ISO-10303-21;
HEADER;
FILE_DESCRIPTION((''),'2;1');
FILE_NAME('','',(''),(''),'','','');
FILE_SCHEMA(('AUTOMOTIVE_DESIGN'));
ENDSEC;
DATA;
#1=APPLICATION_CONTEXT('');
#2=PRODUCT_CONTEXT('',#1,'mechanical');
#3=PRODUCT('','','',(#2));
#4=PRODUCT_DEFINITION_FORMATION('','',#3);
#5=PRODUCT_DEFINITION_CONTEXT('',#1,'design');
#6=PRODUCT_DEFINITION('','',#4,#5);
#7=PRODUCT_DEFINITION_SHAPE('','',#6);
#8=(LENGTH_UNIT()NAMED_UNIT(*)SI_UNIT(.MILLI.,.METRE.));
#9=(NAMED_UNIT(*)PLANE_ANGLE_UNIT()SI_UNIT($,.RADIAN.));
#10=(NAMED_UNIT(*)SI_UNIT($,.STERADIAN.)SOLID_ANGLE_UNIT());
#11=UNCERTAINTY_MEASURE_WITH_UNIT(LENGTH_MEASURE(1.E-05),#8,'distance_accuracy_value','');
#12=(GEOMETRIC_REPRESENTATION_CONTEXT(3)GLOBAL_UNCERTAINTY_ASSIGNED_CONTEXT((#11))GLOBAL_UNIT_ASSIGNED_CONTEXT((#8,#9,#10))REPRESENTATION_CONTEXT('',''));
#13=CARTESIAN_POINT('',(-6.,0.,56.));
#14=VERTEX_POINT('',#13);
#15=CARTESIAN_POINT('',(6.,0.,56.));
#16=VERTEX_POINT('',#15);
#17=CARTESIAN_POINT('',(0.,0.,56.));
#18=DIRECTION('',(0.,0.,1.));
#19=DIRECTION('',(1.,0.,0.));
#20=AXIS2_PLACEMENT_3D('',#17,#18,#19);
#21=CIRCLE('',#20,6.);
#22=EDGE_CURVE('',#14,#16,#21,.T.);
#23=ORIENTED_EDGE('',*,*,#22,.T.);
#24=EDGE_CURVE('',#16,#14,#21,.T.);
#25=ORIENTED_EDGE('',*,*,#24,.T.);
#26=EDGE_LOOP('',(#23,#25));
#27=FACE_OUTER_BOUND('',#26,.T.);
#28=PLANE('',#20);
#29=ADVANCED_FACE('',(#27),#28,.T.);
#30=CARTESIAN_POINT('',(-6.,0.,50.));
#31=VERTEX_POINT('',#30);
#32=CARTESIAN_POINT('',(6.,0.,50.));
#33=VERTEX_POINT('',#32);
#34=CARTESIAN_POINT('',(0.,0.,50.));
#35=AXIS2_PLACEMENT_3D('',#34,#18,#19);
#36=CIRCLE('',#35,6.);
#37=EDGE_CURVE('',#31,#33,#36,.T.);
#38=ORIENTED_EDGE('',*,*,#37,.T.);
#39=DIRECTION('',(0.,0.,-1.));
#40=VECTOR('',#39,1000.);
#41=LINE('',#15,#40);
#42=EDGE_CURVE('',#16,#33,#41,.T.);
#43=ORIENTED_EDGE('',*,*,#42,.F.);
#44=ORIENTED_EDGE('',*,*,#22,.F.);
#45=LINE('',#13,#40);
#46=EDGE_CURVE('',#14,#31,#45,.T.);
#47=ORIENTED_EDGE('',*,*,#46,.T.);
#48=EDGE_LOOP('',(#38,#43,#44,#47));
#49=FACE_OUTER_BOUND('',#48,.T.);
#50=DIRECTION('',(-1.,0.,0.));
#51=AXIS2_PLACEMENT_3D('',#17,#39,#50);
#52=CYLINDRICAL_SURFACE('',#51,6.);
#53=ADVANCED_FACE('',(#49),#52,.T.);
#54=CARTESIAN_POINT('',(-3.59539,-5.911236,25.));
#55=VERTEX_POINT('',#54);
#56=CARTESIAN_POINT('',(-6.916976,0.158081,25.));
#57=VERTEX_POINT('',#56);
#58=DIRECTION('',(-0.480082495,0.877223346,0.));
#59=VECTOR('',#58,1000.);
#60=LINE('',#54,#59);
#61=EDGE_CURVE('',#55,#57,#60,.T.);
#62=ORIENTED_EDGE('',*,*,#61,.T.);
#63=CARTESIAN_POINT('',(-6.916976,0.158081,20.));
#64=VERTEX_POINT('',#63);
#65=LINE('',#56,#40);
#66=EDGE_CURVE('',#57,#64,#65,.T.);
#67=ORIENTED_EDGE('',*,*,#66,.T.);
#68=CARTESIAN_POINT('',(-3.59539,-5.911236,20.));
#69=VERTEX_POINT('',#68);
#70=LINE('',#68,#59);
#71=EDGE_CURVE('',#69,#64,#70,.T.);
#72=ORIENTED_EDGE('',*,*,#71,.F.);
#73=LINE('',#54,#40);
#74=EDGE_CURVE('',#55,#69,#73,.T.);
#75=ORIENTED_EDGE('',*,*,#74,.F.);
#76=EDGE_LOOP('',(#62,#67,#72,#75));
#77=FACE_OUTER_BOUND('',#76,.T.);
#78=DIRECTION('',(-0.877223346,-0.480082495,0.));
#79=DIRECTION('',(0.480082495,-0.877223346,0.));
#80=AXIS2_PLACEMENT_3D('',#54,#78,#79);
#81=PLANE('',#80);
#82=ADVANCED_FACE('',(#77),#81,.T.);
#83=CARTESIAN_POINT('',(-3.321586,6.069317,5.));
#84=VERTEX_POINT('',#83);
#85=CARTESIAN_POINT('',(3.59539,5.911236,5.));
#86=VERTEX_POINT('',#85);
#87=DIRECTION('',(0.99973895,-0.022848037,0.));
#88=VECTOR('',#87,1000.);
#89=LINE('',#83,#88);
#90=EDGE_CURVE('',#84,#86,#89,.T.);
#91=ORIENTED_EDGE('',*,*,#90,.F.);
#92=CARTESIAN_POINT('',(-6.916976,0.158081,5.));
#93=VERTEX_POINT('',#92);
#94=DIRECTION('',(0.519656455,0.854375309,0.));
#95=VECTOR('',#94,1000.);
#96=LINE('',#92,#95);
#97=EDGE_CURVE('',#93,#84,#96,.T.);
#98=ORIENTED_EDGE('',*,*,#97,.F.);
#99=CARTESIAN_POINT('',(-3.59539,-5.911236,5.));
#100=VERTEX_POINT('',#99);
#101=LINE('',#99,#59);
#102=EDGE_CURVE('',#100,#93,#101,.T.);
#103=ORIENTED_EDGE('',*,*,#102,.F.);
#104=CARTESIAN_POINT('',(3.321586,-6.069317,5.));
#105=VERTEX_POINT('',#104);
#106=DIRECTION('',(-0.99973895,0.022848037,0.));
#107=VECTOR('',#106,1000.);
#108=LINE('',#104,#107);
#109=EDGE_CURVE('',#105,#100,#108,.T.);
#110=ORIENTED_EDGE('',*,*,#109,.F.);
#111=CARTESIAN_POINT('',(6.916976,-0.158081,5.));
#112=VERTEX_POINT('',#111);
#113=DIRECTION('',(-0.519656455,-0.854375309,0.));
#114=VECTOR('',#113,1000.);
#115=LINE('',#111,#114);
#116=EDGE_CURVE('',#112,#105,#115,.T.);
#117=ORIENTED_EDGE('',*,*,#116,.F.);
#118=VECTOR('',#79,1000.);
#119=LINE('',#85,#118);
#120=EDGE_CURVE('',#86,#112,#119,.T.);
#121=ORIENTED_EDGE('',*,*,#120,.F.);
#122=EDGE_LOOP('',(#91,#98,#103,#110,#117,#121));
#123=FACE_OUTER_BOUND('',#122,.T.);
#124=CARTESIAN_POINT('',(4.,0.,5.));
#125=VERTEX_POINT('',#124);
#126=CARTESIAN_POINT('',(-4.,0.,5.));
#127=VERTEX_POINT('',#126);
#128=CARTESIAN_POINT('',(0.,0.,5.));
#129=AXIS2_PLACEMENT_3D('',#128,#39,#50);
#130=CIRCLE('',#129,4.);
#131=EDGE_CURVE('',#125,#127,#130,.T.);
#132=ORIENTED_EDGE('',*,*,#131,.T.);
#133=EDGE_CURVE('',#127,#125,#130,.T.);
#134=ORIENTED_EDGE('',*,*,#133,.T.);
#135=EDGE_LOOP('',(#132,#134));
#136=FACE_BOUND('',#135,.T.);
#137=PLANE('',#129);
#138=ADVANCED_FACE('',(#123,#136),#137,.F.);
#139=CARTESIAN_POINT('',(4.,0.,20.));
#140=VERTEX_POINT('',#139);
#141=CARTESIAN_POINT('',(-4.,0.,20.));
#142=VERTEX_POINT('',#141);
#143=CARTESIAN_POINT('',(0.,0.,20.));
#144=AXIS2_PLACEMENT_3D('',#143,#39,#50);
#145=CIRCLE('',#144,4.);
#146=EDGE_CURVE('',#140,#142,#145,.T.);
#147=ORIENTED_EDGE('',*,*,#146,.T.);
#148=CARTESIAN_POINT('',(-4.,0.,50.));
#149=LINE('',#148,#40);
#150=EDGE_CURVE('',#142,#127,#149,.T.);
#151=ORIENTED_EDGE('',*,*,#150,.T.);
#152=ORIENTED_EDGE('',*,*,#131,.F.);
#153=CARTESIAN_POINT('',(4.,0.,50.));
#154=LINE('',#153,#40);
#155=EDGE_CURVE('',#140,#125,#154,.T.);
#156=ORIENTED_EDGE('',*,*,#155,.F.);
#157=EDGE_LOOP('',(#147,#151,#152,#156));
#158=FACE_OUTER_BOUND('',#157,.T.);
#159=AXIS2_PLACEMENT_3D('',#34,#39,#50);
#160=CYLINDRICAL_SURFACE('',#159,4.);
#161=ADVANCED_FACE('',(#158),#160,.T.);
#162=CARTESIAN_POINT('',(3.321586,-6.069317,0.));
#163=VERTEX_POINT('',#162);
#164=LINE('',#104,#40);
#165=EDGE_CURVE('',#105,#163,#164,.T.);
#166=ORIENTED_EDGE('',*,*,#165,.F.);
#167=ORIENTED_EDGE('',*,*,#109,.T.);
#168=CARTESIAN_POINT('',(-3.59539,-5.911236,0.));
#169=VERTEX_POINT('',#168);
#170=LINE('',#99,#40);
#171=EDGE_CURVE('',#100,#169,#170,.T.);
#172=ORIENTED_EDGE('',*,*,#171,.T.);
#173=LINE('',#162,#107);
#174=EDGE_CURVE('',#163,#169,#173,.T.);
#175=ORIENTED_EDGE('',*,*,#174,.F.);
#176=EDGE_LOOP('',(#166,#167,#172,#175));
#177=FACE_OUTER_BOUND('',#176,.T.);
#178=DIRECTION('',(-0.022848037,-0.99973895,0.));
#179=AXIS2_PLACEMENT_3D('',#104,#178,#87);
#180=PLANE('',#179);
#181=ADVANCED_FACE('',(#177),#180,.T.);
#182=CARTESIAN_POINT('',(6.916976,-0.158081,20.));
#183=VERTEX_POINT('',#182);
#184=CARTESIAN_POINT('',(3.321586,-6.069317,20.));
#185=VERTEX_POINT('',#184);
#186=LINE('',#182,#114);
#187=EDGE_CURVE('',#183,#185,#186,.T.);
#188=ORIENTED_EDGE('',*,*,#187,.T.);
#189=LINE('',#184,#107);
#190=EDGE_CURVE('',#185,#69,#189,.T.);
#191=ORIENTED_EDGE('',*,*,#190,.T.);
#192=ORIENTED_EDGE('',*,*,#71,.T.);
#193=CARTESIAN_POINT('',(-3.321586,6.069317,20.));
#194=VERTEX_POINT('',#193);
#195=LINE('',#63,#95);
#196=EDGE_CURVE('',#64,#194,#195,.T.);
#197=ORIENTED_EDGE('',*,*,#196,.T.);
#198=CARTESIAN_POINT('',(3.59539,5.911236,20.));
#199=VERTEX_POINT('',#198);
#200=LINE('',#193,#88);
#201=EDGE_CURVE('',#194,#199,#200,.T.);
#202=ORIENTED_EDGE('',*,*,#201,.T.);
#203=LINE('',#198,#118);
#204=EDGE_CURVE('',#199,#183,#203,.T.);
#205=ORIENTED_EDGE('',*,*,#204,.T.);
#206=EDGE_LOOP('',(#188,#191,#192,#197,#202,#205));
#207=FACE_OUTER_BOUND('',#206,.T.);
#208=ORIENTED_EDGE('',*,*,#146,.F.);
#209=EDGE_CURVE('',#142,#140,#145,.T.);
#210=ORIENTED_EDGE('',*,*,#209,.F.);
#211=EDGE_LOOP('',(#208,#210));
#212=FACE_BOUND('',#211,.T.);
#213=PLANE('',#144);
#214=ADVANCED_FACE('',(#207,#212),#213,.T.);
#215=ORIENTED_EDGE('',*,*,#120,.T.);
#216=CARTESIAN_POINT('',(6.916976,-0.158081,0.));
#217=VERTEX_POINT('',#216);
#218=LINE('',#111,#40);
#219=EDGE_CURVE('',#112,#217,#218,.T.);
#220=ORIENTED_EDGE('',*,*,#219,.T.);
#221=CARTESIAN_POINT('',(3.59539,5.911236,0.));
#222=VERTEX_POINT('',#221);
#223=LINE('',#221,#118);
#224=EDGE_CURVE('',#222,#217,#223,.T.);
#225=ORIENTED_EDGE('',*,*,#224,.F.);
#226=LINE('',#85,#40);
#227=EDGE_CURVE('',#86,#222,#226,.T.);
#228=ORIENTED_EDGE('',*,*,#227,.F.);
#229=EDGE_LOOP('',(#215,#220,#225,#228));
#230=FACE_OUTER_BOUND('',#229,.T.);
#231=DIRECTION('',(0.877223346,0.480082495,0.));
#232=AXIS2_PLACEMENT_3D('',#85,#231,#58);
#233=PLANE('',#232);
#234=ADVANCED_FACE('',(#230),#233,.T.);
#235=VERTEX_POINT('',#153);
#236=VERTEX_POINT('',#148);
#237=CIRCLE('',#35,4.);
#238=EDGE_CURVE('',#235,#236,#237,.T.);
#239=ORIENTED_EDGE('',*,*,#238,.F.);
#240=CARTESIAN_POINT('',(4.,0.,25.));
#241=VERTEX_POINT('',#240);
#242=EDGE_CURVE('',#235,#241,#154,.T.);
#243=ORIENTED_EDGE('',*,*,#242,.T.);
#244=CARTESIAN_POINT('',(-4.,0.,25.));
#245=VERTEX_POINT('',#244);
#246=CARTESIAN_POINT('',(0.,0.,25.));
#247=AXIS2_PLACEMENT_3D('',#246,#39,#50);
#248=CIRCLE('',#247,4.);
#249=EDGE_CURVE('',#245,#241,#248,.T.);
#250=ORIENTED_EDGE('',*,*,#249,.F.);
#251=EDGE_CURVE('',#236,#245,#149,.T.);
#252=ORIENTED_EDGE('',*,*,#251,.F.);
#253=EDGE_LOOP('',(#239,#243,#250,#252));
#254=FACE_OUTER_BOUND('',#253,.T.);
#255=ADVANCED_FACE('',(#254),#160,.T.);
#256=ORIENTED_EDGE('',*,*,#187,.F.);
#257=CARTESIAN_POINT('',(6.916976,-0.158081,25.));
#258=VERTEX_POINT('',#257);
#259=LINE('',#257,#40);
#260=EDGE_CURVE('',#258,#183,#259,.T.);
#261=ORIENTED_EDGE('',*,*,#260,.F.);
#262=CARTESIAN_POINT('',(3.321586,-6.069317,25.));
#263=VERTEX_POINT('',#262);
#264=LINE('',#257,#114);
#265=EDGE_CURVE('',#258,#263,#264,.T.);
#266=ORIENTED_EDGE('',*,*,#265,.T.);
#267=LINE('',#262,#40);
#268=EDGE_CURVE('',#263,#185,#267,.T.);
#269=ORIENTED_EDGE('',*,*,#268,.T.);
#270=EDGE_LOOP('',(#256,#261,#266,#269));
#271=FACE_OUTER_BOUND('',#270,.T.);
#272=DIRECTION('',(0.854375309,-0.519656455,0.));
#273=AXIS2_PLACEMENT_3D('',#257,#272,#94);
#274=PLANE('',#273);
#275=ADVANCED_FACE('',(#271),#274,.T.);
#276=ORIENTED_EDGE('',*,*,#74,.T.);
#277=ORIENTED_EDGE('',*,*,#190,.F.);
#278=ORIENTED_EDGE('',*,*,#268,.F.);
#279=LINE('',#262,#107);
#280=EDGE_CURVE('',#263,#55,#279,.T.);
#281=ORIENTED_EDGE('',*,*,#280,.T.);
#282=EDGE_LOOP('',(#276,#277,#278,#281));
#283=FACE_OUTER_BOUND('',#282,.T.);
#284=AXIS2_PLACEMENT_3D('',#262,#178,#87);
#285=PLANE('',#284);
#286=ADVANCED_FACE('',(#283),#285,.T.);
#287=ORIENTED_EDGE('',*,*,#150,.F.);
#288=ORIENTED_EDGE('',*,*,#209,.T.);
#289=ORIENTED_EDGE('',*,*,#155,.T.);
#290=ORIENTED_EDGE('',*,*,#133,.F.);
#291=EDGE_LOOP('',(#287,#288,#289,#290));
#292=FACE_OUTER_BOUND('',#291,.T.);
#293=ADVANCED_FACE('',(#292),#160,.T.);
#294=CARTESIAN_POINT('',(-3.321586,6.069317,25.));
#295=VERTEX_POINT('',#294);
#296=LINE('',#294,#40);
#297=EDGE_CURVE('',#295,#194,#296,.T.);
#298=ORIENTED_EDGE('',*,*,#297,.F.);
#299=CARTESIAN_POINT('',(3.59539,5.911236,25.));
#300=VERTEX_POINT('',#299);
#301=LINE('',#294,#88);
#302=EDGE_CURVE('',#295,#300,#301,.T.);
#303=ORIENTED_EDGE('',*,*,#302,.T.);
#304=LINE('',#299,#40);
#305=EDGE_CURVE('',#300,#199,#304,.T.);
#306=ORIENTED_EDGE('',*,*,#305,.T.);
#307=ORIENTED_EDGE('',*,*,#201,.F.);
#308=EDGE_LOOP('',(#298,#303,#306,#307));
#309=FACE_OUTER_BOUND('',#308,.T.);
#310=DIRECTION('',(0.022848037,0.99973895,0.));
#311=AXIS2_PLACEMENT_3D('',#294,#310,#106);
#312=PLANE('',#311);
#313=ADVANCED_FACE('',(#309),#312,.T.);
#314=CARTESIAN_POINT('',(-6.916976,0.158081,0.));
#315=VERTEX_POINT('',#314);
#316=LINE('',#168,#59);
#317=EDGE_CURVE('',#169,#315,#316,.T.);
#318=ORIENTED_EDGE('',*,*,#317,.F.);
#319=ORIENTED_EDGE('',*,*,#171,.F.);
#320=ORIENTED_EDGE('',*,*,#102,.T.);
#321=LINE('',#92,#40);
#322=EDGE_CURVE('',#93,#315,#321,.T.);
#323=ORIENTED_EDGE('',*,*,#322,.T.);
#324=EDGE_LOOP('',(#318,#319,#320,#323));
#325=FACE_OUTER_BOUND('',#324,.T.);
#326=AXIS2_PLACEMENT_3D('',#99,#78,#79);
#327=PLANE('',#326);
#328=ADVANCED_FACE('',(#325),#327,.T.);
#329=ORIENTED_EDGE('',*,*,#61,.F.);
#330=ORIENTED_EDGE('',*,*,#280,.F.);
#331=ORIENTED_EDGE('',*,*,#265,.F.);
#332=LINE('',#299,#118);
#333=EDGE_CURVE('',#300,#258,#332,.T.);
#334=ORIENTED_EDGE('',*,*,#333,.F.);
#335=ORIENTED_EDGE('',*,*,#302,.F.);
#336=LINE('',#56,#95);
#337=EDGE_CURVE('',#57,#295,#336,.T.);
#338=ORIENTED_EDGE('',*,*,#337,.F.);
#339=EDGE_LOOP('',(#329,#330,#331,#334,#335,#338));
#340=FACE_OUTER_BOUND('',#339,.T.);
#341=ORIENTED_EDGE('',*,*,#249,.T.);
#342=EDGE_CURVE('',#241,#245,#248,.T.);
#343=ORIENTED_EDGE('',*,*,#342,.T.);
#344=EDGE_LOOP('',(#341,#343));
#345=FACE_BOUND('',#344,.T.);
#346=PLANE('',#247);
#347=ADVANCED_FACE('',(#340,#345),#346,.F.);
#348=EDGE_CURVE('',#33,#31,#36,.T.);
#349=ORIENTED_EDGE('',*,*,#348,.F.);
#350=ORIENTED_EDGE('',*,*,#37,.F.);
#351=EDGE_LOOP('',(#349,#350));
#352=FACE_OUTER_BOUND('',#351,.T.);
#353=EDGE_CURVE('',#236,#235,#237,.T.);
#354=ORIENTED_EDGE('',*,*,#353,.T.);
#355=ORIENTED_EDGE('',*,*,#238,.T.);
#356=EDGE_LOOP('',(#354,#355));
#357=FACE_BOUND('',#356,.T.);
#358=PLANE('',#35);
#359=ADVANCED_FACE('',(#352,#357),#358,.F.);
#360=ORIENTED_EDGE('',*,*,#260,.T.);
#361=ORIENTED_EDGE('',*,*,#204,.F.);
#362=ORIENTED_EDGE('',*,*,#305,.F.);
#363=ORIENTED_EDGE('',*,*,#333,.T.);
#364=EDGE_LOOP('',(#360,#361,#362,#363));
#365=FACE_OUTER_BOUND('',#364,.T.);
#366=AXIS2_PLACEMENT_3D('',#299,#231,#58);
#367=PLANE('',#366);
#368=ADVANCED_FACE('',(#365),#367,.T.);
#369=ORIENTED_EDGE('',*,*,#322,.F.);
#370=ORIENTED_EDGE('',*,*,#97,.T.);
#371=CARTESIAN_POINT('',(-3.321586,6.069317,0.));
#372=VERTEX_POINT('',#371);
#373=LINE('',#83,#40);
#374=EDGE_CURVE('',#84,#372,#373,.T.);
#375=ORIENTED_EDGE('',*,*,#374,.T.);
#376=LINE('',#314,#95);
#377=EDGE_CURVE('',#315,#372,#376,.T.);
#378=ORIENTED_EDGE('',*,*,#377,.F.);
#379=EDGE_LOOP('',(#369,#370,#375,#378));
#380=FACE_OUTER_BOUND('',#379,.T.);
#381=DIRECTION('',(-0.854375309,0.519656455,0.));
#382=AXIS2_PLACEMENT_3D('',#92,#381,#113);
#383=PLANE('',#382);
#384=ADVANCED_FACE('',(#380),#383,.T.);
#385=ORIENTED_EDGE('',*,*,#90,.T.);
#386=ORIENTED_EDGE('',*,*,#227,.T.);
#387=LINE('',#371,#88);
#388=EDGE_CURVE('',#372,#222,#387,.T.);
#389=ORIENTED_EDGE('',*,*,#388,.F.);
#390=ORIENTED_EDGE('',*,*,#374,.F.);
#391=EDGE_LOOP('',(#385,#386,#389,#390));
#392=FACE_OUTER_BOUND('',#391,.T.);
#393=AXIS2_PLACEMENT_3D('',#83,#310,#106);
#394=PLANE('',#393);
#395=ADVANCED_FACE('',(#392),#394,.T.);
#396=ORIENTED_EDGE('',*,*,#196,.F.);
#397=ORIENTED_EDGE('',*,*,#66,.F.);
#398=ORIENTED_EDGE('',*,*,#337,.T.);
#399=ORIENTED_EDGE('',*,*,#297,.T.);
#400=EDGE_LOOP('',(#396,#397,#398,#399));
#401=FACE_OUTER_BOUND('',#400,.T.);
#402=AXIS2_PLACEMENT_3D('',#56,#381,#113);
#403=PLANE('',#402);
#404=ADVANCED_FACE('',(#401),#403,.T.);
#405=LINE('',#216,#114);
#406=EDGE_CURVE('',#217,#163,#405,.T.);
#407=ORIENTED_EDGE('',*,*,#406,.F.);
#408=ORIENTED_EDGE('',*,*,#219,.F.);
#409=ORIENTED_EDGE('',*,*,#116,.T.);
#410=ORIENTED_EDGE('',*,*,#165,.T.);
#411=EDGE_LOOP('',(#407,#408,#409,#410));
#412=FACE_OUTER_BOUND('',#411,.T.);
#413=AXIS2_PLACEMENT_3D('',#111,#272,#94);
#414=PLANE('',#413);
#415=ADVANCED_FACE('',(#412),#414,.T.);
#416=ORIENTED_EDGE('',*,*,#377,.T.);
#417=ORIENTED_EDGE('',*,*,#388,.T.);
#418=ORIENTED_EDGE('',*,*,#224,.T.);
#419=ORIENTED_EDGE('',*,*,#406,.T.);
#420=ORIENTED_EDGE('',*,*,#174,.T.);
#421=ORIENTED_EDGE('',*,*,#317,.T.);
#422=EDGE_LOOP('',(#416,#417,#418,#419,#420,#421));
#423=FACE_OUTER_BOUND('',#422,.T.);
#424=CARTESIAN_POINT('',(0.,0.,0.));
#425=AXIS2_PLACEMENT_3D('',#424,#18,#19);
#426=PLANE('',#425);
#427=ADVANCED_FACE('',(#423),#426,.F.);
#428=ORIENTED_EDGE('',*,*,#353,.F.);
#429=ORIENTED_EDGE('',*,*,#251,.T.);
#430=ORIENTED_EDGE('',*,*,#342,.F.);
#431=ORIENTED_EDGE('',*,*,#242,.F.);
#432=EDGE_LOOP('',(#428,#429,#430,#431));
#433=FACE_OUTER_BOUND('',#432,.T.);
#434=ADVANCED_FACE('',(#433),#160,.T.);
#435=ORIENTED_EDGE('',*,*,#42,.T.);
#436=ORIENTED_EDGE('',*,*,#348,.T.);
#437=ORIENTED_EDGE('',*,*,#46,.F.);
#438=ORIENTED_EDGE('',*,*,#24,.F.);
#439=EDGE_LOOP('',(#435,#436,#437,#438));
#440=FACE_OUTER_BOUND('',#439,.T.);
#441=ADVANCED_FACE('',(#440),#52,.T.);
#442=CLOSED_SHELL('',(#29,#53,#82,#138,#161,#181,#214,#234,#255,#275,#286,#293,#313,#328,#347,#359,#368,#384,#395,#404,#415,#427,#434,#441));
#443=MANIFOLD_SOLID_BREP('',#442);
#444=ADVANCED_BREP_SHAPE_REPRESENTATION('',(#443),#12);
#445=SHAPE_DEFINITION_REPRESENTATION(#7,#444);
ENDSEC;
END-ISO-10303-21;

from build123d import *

# Parameters (mm, degrees)
SKETCH1_R           = 4
BOSS_EXTRUDE1_DEPTH = 50
SKETCH2_R           = 6
BOSS_EXTRUDE2_DEPTH = 6
BOSS_EXTRUDE3_DEPTH = 5
LPATTERN1_COUNT     = 2
LPATTERN1_PITCH     = 20


with BuildPart() as part:
    # Sketch1 → Boss-Extrude1 (new body)
    with BuildSketch(Plane.XY):
        Circle(SKETCH1_R)
    extrude(amount=BOSS_EXTRUDE1_DEPTH)

    # Sketch2 → Boss-Extrude2 (add)
    with BuildSketch(Plane.XY.offset(50)):
        Circle(SKETCH2_R)
    extrude(amount=BOSS_EXTRUDE2_DEPTH)

    # Sketch3 → Boss-Extrude3 (add)
    with BuildSketch(Plane(origin=(0, 0, 0), x_dir=(-1, 0, 0), z_dir=(0, 0, -1))):
        Polygon((3.321586055, 6.06931697), (-3.595389652, 5.911236389), (-6.916975707, -0.158080581), (-3.321586055, -6.06931697), (3.595389652, -5.911236389), (6.916975707, 0.158080581), align=None)
    boss_extrude3 = extrude(amount=-BOSS_EXTRUDE3_DEPTH)

    # LPattern1: Boss-Extrude3 ×2
    with Locations(*[(0, 0, i * LPATTERN1_PITCH) for i in range(1, LPATTERN1_COUNT)]):
        add(boss_extrude3)


solid = part.part
